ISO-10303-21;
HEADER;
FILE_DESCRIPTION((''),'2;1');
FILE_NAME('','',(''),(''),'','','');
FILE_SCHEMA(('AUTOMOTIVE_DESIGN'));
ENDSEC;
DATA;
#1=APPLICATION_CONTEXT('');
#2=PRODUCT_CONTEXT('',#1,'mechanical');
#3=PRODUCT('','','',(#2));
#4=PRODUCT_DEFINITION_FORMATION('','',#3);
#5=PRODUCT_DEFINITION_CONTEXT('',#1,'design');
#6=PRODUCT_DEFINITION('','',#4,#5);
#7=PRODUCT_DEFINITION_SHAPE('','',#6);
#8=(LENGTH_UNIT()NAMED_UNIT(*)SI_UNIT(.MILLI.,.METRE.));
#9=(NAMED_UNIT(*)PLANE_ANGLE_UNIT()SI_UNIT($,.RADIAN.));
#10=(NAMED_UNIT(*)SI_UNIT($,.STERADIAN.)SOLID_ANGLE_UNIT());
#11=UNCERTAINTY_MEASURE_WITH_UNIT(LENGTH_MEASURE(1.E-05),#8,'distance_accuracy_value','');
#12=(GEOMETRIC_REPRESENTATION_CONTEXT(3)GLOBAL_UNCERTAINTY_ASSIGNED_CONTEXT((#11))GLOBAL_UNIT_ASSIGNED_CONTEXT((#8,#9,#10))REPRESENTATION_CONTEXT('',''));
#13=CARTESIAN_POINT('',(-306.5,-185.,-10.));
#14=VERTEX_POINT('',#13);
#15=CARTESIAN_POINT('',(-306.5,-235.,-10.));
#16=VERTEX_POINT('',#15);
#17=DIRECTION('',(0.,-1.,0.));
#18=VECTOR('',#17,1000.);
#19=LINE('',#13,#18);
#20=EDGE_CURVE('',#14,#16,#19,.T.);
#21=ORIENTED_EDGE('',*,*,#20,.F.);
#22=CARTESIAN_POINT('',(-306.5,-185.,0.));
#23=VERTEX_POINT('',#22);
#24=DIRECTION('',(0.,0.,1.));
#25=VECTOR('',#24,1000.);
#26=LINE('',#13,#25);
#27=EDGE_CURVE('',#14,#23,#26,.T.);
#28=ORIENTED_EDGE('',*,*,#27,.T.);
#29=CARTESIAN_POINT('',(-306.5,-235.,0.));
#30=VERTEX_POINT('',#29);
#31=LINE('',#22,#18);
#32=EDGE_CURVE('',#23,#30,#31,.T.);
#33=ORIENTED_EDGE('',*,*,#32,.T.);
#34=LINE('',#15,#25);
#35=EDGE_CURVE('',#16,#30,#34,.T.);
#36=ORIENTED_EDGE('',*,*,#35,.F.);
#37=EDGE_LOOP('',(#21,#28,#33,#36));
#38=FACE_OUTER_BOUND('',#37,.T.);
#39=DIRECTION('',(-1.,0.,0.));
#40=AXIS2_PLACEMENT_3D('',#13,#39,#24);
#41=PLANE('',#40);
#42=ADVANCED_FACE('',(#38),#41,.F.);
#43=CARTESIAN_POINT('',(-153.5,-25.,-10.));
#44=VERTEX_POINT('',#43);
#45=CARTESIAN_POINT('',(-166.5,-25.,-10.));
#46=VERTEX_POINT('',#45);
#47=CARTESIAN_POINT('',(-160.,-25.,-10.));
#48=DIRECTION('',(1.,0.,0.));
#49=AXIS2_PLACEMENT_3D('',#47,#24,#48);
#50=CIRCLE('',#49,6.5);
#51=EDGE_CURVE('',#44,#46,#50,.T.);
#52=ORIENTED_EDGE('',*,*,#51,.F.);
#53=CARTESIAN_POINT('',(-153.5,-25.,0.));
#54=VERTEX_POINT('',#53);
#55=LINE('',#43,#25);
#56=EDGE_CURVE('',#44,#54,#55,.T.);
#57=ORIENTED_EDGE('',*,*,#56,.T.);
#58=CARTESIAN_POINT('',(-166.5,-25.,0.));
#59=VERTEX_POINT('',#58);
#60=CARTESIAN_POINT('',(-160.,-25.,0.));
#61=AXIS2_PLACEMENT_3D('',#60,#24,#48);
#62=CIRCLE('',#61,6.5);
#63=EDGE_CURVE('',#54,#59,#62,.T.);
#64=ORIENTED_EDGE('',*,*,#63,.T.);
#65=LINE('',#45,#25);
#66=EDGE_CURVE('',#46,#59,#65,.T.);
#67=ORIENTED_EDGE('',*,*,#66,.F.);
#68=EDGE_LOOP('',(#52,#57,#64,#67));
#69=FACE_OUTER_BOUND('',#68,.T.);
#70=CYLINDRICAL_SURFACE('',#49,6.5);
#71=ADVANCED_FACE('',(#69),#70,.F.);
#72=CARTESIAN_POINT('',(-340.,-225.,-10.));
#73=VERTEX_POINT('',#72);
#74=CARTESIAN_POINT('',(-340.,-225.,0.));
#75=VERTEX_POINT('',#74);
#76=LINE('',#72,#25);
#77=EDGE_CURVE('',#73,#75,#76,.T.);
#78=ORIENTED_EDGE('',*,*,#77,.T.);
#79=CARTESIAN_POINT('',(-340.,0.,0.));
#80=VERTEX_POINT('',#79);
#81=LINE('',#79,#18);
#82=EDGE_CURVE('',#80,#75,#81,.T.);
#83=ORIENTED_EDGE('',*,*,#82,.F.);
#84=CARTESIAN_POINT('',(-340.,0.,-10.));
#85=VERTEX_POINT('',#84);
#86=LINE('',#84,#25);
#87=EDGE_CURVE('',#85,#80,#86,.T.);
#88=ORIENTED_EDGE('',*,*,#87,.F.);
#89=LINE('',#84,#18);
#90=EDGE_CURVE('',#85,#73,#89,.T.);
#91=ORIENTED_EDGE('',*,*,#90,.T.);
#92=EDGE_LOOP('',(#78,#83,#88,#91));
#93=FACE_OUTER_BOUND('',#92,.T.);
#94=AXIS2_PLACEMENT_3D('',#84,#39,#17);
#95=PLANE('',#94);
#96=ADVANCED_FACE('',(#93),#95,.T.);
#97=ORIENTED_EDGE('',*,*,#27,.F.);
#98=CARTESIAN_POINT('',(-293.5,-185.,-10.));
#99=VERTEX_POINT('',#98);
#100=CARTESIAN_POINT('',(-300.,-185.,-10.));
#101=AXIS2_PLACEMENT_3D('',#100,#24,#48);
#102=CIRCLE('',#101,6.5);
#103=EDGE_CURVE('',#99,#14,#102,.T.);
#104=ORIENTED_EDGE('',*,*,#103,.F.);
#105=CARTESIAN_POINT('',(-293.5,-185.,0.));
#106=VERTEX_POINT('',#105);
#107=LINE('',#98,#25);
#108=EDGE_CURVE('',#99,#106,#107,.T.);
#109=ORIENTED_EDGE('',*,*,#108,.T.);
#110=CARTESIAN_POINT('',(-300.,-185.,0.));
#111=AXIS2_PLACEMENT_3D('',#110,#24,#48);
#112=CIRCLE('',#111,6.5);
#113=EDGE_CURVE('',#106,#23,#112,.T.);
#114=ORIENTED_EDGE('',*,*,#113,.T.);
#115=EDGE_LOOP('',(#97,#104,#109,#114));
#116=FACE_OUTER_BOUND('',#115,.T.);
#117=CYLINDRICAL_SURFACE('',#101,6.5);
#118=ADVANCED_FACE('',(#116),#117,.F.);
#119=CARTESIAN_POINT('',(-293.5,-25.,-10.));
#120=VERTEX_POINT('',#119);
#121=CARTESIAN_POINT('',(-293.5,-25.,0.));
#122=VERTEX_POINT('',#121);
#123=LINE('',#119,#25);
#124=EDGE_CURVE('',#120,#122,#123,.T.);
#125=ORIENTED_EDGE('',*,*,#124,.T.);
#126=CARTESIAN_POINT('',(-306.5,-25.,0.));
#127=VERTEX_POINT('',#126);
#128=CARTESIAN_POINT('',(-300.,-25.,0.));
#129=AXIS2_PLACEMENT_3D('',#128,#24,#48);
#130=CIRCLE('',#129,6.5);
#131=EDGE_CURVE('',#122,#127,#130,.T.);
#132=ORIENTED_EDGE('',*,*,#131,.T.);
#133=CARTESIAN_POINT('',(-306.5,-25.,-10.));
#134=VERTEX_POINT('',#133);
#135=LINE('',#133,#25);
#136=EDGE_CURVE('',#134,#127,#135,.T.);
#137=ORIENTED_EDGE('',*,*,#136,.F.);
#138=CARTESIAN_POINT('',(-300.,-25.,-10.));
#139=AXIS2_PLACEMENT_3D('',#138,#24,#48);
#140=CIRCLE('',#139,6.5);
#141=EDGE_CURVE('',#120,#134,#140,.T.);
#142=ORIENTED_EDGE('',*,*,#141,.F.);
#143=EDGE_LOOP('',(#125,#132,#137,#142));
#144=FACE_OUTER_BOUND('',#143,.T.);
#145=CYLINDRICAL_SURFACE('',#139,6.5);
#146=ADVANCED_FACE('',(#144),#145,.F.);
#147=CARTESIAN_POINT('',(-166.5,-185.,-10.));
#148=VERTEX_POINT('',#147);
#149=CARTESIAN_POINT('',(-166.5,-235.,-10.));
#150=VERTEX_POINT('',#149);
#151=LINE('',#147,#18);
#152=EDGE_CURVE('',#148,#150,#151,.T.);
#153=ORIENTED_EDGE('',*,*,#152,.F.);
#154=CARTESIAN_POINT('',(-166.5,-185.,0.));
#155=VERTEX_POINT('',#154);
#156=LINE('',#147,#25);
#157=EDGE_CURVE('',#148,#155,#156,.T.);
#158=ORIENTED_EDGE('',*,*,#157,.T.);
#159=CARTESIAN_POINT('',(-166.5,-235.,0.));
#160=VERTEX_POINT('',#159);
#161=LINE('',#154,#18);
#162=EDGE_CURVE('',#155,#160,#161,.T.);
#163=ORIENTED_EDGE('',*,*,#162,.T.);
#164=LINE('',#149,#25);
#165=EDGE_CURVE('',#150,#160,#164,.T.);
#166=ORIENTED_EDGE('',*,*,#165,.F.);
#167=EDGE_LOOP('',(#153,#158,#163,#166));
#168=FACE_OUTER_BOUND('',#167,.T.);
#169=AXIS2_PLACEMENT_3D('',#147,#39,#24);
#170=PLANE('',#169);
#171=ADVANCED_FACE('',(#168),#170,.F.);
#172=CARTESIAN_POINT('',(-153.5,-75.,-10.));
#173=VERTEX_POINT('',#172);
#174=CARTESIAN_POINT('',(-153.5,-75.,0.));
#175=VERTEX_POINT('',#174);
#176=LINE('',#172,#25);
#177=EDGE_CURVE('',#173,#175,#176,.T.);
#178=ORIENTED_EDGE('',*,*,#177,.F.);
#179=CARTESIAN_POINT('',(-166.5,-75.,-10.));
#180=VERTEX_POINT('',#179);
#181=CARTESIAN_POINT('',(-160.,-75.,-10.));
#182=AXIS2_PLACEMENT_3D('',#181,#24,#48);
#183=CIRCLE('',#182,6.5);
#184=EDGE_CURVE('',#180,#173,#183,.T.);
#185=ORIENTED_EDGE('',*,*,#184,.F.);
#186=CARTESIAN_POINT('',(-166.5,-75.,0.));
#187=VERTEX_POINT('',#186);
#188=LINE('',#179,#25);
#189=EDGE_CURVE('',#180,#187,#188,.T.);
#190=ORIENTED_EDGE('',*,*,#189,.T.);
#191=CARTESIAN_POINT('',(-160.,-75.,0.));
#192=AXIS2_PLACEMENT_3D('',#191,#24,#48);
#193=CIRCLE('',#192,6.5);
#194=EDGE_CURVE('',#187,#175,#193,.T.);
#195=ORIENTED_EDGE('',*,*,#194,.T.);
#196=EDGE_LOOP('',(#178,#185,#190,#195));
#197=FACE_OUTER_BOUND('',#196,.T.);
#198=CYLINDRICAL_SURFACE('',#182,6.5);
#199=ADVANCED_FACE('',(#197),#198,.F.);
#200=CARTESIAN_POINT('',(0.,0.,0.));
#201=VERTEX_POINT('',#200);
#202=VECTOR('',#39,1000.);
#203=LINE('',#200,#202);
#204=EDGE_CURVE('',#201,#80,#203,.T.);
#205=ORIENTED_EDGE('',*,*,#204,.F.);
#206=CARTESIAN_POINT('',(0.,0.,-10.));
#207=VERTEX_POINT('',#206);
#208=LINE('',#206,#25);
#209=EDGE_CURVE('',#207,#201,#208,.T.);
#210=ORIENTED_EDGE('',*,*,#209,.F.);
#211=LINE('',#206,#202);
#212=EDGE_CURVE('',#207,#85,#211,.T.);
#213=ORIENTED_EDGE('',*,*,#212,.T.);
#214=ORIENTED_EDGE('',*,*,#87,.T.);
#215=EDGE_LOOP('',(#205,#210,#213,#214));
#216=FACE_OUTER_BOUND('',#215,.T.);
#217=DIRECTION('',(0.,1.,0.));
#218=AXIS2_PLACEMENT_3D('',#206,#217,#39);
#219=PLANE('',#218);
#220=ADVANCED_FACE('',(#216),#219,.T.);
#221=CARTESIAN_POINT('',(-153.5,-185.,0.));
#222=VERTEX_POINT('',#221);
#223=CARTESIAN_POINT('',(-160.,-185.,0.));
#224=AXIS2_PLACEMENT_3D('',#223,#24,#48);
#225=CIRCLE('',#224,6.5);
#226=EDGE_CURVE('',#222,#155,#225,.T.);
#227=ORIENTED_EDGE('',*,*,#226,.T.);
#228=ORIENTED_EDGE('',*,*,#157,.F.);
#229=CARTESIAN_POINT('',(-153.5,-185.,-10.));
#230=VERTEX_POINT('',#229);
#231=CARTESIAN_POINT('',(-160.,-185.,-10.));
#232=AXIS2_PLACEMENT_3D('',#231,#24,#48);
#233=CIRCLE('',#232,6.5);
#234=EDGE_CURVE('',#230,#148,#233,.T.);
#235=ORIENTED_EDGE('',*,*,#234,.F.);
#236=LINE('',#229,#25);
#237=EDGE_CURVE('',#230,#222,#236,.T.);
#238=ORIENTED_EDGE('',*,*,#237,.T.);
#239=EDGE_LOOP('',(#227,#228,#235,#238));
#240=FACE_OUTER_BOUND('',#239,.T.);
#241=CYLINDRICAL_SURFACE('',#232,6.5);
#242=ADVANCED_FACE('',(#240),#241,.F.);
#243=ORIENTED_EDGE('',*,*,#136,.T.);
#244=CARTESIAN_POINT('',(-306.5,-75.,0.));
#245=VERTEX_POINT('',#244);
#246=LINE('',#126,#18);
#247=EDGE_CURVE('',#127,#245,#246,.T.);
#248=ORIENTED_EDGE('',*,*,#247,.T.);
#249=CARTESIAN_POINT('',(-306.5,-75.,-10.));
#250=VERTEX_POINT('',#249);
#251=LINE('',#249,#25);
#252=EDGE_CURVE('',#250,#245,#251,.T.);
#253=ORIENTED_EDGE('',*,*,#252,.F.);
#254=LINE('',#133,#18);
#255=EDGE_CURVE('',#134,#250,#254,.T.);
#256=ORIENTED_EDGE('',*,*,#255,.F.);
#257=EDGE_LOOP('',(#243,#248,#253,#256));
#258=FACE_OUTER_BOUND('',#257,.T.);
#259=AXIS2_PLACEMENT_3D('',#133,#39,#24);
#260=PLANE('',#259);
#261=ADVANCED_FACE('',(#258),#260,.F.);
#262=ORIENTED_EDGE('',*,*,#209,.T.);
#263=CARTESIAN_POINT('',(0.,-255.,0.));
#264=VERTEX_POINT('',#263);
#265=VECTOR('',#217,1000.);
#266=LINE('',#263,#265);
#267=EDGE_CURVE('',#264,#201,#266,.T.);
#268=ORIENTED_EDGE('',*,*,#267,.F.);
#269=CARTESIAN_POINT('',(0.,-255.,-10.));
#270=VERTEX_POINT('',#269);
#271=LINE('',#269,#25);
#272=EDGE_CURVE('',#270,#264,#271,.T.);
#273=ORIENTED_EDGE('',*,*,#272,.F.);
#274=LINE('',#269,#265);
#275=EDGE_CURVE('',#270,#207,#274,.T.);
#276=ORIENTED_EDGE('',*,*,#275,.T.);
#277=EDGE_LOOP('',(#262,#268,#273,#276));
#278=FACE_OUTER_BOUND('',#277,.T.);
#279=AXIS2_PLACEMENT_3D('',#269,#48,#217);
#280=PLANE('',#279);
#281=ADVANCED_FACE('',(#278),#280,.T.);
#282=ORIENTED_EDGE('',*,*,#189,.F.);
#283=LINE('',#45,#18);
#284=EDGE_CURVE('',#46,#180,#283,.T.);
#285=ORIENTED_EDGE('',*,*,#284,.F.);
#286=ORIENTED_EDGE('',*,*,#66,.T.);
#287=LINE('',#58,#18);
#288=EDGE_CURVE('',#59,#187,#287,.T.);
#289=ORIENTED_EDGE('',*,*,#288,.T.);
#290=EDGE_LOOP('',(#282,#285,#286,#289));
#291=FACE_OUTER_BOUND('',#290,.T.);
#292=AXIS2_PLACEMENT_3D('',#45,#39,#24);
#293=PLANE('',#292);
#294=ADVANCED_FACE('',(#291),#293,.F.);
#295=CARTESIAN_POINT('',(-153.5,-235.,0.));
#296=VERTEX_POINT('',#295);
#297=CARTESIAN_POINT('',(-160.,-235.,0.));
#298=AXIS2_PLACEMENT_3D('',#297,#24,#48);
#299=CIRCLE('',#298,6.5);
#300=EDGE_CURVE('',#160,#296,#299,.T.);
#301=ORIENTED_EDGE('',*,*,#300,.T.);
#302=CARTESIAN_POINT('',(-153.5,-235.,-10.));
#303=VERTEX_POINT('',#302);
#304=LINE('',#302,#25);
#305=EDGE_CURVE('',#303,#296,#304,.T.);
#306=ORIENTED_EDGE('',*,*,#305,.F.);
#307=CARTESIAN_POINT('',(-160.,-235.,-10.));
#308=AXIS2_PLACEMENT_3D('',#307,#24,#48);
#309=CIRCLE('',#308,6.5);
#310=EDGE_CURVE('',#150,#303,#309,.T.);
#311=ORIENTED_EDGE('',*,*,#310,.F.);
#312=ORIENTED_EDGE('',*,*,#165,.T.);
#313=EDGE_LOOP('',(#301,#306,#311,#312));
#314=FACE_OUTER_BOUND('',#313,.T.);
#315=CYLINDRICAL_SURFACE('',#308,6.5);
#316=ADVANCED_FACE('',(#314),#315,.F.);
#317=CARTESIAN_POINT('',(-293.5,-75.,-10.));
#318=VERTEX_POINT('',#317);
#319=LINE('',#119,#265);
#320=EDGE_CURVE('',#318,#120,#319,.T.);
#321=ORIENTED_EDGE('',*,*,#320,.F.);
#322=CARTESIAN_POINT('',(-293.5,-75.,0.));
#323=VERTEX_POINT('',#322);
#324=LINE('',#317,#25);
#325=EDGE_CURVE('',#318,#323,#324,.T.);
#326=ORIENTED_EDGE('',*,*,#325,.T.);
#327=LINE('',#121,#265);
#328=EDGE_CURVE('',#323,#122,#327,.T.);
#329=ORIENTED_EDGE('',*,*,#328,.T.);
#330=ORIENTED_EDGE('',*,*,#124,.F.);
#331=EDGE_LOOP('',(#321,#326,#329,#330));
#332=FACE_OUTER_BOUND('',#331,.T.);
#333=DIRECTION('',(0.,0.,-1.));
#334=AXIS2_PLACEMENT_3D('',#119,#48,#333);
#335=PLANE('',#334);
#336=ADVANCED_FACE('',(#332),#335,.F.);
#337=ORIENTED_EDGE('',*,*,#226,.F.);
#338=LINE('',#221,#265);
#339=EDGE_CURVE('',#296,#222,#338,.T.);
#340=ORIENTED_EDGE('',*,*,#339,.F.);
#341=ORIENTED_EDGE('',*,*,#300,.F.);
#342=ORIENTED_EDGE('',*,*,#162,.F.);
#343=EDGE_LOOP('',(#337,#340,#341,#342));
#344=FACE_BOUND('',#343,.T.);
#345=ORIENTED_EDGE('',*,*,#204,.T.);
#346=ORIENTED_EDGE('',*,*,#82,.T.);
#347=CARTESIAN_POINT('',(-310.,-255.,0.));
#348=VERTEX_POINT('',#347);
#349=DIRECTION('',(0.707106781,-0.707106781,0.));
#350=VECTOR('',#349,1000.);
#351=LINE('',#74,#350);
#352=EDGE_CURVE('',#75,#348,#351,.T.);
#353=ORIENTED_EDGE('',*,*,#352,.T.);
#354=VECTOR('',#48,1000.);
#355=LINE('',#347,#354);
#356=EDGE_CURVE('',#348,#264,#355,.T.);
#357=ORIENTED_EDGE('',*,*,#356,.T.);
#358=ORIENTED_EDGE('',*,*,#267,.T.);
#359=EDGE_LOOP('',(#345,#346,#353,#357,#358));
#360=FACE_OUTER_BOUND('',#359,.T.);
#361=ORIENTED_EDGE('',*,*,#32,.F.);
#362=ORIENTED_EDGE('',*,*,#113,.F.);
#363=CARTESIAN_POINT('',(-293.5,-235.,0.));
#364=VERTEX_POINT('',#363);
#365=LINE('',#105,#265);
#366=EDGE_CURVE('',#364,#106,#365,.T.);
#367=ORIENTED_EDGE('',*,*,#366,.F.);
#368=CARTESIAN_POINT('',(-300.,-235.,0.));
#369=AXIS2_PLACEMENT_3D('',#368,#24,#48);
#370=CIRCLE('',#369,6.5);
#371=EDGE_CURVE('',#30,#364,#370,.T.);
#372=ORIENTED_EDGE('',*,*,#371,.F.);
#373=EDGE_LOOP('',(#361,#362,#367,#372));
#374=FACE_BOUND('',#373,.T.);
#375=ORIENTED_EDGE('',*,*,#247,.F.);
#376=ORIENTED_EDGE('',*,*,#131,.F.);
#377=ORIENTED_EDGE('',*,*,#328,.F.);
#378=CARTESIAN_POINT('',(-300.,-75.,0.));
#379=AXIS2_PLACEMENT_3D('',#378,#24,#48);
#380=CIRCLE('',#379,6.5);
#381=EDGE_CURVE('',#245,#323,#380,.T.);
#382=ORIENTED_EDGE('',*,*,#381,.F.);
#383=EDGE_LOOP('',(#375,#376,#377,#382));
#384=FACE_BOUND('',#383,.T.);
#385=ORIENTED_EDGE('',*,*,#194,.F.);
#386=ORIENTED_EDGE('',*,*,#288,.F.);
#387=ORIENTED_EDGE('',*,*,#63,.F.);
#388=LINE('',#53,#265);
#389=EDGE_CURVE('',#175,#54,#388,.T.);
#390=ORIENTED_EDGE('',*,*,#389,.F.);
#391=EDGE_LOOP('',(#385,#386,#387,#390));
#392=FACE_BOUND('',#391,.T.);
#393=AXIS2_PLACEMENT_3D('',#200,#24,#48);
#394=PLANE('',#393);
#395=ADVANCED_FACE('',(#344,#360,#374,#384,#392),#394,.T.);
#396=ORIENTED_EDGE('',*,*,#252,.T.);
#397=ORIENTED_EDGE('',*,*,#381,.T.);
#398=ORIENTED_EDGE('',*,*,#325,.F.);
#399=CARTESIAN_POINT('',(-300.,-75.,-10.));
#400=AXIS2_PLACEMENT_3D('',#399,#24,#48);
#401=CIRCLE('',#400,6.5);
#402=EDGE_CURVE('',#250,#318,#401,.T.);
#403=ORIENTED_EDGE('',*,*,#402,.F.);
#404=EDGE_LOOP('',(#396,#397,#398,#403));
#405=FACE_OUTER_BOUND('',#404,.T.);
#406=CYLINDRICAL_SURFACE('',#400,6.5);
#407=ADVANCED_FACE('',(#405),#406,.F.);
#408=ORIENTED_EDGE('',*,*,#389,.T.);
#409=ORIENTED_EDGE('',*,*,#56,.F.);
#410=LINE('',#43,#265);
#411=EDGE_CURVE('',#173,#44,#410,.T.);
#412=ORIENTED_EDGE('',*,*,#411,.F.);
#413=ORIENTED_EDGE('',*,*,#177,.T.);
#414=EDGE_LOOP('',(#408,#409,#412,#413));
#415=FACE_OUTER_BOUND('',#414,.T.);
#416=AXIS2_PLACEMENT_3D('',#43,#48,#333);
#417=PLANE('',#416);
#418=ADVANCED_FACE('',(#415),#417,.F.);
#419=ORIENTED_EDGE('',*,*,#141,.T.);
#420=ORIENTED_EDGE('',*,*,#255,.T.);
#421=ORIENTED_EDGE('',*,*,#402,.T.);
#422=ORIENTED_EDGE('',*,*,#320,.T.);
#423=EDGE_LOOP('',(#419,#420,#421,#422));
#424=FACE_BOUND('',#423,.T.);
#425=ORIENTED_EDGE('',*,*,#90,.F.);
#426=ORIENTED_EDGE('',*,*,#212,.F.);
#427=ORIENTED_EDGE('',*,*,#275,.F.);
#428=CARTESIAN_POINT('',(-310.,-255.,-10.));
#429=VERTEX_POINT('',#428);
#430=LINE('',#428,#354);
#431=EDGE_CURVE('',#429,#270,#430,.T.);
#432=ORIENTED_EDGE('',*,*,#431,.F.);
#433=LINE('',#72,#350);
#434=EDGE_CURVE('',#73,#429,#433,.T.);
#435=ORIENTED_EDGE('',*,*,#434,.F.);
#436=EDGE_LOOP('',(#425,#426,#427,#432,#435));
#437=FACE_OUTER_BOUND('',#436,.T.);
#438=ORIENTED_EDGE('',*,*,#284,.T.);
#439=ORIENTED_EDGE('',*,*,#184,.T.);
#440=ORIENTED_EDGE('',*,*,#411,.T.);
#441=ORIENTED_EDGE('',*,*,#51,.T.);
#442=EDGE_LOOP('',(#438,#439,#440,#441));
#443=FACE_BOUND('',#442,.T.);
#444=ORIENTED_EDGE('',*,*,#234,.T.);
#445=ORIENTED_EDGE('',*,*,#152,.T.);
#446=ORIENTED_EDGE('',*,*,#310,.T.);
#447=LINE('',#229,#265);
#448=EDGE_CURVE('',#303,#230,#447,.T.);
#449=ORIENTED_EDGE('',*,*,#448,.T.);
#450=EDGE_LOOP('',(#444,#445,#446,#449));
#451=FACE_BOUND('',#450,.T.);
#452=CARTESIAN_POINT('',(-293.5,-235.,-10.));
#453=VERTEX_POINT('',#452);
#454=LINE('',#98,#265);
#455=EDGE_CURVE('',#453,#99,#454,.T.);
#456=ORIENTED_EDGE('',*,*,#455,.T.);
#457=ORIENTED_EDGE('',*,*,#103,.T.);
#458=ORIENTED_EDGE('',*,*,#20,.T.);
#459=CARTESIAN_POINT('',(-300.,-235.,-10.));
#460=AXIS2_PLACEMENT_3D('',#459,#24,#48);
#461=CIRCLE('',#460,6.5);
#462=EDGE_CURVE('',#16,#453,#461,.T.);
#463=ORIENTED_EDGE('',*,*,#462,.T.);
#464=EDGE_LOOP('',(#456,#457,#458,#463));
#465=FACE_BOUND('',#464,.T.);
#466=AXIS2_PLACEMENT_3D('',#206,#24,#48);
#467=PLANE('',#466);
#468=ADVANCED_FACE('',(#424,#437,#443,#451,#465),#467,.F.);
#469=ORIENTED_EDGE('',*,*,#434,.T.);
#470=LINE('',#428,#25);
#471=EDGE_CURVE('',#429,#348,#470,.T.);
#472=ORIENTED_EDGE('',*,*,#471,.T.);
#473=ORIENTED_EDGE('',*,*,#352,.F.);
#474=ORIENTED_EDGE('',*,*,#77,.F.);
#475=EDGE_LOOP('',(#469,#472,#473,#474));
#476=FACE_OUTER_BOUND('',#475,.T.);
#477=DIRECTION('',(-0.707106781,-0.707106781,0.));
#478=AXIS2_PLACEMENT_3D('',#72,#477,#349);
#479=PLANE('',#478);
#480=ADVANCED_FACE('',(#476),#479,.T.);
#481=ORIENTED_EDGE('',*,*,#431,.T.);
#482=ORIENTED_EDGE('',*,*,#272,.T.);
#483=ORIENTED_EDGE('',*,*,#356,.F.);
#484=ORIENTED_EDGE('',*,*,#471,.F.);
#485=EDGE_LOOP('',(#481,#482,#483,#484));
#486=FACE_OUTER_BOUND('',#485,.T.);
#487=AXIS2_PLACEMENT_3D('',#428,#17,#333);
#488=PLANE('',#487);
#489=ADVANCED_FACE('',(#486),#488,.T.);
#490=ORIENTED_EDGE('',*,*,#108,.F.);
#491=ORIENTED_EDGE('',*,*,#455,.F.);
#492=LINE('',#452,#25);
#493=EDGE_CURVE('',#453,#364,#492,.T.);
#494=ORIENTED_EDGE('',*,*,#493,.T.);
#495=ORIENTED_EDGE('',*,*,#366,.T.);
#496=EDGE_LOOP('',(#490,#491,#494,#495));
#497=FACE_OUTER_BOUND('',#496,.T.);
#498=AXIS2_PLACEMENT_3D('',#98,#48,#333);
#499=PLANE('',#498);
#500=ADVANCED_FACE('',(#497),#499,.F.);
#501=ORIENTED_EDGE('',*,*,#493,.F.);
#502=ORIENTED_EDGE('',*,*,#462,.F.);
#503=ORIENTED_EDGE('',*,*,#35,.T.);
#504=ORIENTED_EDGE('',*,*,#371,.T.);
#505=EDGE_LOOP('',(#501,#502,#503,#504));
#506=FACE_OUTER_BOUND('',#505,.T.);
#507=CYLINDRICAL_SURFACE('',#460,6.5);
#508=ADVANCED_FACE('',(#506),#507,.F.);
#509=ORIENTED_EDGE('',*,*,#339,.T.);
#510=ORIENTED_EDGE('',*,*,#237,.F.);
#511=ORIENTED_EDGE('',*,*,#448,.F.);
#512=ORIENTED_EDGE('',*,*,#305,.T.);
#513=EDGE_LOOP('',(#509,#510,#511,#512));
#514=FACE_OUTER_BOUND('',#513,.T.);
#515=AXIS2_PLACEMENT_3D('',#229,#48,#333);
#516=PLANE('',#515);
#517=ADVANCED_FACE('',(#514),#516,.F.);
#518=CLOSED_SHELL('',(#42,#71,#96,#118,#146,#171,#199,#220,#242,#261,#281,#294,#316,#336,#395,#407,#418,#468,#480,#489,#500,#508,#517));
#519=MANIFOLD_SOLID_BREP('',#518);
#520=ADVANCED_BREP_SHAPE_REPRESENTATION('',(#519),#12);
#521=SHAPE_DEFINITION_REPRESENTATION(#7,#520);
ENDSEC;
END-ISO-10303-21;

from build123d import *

# Parameters (mm, degrees)
BOSS_EXTRUDE1_DEPTH = 10


with BuildPart() as part:
    # Sketch1 → Boss-Extrude1 (new body)
    with BuildSketch(Plane.XY):
        Polygon((0, 0), (-340, 0), (-340, -225), (-310, -255), (0, -255), align=None)
        with BuildLine():
            Line((-293.5, -25), (-293.5, -75))
            ThreePointArc((-293.5, -75), (-300, -81.5), (-306.5, -75))
            Line((-306.5, -75), (-306.5, -25))
            ThreePointArc((-306.5, -25), (-300, -18.5), (-293.5, -25))
        make_face(mode=Mode.SUBTRACT)
        with BuildLine():
            Line((-153.5, -25), (-153.5, -75))
            ThreePointArc((-153.5, -75), (-160, -81.5), (-166.5, -75))
            Line((-166.5, -75), (-166.5, -25))
            ThreePointArc((-166.5, -25), (-160, -18.5), (-153.5, -25))
        make_face(mode=Mode.SUBTRACT)
        with BuildLine():
            Line((-293.5, -185), (-293.5, -235))
            ThreePointArc((-293.5, -235), (-300, -241.5), (-306.5, -235))
            Line((-306.5, -235), (-306.5, -185))
            ThreePointArc((-306.5, -185), (-300, -178.5), (-293.5, -185))
        make_face(mode=Mode.SUBTRACT)
        with BuildLine():
            Line((-153.5, -185), (-153.5, -235))
            ThreePointArc((-153.5, -235), (-160, -241.5), (-166.5, -235))
            Line((-166.5, -235), (-166.5, -185))
            ThreePointArc((-166.5, -185), (-160, -178.5), (-153.5, -185))
        make_face(mode=Mode.SUBTRACT)
    extrude(amount=-BOSS_EXTRUDE1_DEPTH)


solid = part.part
